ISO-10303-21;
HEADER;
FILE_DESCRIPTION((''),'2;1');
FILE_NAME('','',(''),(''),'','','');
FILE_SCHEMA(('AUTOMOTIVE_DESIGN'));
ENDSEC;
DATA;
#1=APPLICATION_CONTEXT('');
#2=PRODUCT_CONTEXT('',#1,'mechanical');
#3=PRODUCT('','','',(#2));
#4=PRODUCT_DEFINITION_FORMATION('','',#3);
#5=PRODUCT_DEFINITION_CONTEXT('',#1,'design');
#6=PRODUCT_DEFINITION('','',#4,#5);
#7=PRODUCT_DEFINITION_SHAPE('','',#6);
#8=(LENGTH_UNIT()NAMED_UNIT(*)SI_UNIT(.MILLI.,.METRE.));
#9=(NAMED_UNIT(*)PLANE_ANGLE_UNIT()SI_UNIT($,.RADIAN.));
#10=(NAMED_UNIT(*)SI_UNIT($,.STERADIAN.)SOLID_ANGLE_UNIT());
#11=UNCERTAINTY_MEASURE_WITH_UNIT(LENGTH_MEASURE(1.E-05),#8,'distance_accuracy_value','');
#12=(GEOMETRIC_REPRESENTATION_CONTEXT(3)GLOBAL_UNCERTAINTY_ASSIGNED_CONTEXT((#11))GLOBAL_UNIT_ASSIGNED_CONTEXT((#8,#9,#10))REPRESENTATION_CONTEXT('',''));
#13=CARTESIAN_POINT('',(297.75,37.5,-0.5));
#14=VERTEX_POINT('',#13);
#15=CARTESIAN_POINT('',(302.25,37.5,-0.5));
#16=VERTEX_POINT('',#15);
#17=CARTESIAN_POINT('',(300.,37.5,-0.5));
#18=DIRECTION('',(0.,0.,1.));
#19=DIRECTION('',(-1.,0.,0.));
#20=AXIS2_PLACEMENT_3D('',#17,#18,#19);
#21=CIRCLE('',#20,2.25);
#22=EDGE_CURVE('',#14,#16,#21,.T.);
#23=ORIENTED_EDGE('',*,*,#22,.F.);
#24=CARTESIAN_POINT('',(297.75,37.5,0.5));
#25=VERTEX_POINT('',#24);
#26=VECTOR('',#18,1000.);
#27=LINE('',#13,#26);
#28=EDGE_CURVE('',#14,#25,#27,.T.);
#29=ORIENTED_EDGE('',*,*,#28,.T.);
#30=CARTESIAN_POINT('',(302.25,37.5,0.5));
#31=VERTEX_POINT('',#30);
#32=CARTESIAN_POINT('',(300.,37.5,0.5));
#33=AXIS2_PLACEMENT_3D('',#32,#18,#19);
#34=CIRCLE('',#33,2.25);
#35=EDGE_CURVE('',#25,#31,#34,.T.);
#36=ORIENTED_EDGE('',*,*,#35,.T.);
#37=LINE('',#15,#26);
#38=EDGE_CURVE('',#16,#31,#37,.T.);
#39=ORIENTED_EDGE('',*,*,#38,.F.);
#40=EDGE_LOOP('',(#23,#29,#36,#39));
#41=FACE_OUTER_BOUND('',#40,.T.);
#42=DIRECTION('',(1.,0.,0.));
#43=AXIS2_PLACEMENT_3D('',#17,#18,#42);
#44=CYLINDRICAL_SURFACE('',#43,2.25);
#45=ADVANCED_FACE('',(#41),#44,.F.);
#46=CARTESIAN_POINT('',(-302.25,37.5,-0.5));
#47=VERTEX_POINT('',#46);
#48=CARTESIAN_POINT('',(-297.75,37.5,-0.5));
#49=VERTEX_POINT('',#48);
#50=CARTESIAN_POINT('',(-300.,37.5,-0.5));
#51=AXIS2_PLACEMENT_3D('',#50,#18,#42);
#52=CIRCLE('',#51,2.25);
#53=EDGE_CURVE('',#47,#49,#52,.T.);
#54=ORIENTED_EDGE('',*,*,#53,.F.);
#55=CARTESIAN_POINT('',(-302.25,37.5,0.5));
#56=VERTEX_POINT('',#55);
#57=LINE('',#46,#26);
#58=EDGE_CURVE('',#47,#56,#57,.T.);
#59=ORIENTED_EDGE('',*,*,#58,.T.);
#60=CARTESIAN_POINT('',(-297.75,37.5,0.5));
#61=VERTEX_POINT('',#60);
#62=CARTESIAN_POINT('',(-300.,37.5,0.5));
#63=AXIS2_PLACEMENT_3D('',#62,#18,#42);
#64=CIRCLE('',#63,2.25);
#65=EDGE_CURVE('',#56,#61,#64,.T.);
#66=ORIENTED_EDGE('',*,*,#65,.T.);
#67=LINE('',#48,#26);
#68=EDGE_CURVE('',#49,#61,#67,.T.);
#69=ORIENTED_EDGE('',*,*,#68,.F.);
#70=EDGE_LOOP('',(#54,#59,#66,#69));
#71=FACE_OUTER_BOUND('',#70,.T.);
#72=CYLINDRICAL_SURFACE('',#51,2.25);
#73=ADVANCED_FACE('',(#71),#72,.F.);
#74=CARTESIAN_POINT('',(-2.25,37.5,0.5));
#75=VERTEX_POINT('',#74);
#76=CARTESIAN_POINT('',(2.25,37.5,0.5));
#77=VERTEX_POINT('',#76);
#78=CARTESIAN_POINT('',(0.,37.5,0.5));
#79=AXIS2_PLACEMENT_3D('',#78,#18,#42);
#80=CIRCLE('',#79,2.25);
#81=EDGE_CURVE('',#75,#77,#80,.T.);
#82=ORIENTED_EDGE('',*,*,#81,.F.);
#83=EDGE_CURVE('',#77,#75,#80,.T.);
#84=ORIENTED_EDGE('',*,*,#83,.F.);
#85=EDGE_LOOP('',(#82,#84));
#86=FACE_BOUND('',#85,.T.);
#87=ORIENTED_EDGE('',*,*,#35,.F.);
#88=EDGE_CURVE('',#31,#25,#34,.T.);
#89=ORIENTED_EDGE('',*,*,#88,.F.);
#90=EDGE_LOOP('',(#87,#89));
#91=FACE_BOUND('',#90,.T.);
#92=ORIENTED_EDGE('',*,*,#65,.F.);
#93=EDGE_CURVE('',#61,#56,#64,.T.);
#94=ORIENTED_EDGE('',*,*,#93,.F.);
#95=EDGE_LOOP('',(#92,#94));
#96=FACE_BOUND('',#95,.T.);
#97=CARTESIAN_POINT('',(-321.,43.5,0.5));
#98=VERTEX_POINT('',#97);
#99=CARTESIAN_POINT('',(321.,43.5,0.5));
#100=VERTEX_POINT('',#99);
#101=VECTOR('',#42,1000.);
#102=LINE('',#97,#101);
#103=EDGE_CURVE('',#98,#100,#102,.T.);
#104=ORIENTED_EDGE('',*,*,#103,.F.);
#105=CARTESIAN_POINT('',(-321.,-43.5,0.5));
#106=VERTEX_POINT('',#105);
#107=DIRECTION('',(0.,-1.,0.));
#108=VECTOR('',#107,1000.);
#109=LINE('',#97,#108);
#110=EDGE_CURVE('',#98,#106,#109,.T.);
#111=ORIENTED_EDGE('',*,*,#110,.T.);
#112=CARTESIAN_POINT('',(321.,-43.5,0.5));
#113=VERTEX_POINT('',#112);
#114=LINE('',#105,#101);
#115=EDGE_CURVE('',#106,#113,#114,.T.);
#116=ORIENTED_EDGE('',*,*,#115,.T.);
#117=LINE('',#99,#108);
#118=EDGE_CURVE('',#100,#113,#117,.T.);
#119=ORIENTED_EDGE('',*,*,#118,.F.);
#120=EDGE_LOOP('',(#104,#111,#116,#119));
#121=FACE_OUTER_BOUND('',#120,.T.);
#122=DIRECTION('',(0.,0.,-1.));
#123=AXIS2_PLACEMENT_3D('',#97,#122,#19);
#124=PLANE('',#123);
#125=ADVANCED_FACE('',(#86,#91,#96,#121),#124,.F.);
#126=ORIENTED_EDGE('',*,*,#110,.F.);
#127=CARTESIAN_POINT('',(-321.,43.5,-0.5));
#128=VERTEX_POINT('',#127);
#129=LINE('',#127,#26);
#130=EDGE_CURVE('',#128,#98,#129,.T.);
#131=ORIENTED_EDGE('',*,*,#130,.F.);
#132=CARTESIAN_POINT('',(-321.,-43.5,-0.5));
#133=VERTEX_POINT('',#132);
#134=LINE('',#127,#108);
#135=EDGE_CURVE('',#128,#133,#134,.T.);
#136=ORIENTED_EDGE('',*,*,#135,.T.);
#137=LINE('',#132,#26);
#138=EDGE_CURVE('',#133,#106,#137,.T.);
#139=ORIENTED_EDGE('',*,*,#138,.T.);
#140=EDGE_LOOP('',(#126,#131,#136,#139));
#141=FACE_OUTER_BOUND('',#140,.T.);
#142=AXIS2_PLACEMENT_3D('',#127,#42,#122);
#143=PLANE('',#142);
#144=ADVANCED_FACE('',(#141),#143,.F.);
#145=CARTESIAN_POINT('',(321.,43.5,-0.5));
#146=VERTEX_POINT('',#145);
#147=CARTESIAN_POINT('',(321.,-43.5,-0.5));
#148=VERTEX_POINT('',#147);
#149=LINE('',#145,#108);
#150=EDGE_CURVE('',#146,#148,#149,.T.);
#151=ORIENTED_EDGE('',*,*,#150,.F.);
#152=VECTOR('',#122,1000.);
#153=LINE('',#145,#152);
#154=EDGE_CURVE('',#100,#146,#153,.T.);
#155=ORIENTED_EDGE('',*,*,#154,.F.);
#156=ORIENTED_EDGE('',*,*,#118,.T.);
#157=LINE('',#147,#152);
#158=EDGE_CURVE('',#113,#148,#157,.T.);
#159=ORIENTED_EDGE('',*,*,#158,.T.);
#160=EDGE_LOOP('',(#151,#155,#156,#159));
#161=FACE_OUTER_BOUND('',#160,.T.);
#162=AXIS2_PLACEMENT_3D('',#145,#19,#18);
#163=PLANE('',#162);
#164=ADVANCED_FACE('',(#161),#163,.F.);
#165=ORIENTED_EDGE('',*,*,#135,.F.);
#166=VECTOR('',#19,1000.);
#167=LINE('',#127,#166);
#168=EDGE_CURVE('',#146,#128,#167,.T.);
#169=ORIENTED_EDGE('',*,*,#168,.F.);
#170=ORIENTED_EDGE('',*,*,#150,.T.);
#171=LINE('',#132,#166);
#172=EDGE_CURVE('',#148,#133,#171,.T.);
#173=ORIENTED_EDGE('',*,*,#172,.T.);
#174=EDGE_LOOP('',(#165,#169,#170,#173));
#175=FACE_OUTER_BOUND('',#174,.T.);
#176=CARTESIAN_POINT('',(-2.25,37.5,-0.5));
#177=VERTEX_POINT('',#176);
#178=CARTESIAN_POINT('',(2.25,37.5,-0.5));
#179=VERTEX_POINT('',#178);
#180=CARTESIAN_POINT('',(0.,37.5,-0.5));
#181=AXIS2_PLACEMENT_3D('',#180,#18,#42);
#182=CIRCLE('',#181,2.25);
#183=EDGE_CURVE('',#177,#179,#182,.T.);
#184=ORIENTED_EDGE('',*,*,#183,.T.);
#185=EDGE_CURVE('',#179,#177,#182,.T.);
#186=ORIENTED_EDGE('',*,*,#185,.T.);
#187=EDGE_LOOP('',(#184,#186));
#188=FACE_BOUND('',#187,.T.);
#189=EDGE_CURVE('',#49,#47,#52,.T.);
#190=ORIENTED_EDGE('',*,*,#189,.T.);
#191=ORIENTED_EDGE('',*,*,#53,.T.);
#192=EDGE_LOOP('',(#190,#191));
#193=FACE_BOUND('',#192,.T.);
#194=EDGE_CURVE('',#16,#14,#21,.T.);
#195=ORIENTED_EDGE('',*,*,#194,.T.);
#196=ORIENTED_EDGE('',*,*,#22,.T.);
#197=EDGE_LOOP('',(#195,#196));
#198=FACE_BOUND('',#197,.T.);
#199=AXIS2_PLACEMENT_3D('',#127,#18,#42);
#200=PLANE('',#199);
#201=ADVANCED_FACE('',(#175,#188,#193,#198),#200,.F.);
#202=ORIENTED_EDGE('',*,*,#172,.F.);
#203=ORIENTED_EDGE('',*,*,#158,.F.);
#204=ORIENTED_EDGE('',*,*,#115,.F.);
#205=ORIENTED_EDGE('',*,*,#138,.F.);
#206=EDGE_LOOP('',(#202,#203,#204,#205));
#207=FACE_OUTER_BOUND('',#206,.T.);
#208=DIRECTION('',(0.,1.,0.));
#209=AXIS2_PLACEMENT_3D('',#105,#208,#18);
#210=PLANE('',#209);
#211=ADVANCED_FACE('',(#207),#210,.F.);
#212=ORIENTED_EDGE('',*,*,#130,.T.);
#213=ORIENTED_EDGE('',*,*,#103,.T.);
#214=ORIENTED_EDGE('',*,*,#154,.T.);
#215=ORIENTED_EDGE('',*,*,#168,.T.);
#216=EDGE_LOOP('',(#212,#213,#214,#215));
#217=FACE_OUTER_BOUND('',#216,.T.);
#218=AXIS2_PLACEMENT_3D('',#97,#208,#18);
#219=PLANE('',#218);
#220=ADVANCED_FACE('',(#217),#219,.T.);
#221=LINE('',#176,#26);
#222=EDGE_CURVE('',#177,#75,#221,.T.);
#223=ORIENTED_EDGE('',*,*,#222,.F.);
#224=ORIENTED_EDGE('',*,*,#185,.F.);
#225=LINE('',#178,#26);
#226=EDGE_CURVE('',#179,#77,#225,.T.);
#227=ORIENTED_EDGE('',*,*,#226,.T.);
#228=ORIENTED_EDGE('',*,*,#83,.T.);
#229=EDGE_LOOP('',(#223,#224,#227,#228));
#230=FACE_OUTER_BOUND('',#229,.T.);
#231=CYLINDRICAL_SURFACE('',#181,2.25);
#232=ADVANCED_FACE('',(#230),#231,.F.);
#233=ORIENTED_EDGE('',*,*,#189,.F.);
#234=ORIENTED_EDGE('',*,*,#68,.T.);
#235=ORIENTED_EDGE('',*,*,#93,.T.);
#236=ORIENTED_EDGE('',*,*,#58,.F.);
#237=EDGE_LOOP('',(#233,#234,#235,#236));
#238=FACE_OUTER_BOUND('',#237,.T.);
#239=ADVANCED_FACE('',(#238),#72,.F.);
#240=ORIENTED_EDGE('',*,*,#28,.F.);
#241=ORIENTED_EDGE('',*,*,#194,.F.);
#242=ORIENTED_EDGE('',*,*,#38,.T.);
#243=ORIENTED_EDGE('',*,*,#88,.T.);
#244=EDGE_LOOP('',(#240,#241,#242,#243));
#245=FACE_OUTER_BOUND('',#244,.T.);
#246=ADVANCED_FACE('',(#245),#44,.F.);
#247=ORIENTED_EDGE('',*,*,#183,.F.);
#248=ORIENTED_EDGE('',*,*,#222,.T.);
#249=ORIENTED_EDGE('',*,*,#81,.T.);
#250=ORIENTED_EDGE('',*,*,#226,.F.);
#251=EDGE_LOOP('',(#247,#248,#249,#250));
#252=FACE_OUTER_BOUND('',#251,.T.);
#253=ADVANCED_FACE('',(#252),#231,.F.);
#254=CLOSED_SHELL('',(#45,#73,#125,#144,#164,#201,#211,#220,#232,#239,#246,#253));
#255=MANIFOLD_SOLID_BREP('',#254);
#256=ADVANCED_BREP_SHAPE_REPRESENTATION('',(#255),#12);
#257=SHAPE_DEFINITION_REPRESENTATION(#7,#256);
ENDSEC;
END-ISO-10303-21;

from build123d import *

# Parameters (mm, degrees)
SKETCH1_W          = 642
SKETCH1_H          = 1
EXTRUDE1_DEPTH     = 43.5
SKETCH2_R          = 2.25
CUT_EXTRUDE1_DEPTH = 324.93556458


with BuildPart() as part:
    # Sketch1 → Extrude1 (new, symmetric)
    with BuildSketch(Plane(origin=(0, 0, 0), x_dir=(1, 0, 0), z_dir=(0, 1, 0))):
        Rectangle(SKETCH1_W, SKETCH1_H)
    extrude(amount=EXTRUDE1_DEPTH, both=True)

    # Sketch2 → Cut-Extrude1 (cut, through all)
    with BuildSketch(Plane.XY.offset(0.5)):
        with Locations((-300, 37.5)):
            Circle(SKETCH2_R)
        with Locations((0, 37.5)):
            Circle(SKETCH2_R)
        with Locations(Location((300, 37.5, 0), (0, 0, 180))):
            Circle(SKETCH2_R)
    extrude(amount=-CUT_EXTRUDE1_DEPTH, mode=Mode.SUBTRACT)


solid = part.part
